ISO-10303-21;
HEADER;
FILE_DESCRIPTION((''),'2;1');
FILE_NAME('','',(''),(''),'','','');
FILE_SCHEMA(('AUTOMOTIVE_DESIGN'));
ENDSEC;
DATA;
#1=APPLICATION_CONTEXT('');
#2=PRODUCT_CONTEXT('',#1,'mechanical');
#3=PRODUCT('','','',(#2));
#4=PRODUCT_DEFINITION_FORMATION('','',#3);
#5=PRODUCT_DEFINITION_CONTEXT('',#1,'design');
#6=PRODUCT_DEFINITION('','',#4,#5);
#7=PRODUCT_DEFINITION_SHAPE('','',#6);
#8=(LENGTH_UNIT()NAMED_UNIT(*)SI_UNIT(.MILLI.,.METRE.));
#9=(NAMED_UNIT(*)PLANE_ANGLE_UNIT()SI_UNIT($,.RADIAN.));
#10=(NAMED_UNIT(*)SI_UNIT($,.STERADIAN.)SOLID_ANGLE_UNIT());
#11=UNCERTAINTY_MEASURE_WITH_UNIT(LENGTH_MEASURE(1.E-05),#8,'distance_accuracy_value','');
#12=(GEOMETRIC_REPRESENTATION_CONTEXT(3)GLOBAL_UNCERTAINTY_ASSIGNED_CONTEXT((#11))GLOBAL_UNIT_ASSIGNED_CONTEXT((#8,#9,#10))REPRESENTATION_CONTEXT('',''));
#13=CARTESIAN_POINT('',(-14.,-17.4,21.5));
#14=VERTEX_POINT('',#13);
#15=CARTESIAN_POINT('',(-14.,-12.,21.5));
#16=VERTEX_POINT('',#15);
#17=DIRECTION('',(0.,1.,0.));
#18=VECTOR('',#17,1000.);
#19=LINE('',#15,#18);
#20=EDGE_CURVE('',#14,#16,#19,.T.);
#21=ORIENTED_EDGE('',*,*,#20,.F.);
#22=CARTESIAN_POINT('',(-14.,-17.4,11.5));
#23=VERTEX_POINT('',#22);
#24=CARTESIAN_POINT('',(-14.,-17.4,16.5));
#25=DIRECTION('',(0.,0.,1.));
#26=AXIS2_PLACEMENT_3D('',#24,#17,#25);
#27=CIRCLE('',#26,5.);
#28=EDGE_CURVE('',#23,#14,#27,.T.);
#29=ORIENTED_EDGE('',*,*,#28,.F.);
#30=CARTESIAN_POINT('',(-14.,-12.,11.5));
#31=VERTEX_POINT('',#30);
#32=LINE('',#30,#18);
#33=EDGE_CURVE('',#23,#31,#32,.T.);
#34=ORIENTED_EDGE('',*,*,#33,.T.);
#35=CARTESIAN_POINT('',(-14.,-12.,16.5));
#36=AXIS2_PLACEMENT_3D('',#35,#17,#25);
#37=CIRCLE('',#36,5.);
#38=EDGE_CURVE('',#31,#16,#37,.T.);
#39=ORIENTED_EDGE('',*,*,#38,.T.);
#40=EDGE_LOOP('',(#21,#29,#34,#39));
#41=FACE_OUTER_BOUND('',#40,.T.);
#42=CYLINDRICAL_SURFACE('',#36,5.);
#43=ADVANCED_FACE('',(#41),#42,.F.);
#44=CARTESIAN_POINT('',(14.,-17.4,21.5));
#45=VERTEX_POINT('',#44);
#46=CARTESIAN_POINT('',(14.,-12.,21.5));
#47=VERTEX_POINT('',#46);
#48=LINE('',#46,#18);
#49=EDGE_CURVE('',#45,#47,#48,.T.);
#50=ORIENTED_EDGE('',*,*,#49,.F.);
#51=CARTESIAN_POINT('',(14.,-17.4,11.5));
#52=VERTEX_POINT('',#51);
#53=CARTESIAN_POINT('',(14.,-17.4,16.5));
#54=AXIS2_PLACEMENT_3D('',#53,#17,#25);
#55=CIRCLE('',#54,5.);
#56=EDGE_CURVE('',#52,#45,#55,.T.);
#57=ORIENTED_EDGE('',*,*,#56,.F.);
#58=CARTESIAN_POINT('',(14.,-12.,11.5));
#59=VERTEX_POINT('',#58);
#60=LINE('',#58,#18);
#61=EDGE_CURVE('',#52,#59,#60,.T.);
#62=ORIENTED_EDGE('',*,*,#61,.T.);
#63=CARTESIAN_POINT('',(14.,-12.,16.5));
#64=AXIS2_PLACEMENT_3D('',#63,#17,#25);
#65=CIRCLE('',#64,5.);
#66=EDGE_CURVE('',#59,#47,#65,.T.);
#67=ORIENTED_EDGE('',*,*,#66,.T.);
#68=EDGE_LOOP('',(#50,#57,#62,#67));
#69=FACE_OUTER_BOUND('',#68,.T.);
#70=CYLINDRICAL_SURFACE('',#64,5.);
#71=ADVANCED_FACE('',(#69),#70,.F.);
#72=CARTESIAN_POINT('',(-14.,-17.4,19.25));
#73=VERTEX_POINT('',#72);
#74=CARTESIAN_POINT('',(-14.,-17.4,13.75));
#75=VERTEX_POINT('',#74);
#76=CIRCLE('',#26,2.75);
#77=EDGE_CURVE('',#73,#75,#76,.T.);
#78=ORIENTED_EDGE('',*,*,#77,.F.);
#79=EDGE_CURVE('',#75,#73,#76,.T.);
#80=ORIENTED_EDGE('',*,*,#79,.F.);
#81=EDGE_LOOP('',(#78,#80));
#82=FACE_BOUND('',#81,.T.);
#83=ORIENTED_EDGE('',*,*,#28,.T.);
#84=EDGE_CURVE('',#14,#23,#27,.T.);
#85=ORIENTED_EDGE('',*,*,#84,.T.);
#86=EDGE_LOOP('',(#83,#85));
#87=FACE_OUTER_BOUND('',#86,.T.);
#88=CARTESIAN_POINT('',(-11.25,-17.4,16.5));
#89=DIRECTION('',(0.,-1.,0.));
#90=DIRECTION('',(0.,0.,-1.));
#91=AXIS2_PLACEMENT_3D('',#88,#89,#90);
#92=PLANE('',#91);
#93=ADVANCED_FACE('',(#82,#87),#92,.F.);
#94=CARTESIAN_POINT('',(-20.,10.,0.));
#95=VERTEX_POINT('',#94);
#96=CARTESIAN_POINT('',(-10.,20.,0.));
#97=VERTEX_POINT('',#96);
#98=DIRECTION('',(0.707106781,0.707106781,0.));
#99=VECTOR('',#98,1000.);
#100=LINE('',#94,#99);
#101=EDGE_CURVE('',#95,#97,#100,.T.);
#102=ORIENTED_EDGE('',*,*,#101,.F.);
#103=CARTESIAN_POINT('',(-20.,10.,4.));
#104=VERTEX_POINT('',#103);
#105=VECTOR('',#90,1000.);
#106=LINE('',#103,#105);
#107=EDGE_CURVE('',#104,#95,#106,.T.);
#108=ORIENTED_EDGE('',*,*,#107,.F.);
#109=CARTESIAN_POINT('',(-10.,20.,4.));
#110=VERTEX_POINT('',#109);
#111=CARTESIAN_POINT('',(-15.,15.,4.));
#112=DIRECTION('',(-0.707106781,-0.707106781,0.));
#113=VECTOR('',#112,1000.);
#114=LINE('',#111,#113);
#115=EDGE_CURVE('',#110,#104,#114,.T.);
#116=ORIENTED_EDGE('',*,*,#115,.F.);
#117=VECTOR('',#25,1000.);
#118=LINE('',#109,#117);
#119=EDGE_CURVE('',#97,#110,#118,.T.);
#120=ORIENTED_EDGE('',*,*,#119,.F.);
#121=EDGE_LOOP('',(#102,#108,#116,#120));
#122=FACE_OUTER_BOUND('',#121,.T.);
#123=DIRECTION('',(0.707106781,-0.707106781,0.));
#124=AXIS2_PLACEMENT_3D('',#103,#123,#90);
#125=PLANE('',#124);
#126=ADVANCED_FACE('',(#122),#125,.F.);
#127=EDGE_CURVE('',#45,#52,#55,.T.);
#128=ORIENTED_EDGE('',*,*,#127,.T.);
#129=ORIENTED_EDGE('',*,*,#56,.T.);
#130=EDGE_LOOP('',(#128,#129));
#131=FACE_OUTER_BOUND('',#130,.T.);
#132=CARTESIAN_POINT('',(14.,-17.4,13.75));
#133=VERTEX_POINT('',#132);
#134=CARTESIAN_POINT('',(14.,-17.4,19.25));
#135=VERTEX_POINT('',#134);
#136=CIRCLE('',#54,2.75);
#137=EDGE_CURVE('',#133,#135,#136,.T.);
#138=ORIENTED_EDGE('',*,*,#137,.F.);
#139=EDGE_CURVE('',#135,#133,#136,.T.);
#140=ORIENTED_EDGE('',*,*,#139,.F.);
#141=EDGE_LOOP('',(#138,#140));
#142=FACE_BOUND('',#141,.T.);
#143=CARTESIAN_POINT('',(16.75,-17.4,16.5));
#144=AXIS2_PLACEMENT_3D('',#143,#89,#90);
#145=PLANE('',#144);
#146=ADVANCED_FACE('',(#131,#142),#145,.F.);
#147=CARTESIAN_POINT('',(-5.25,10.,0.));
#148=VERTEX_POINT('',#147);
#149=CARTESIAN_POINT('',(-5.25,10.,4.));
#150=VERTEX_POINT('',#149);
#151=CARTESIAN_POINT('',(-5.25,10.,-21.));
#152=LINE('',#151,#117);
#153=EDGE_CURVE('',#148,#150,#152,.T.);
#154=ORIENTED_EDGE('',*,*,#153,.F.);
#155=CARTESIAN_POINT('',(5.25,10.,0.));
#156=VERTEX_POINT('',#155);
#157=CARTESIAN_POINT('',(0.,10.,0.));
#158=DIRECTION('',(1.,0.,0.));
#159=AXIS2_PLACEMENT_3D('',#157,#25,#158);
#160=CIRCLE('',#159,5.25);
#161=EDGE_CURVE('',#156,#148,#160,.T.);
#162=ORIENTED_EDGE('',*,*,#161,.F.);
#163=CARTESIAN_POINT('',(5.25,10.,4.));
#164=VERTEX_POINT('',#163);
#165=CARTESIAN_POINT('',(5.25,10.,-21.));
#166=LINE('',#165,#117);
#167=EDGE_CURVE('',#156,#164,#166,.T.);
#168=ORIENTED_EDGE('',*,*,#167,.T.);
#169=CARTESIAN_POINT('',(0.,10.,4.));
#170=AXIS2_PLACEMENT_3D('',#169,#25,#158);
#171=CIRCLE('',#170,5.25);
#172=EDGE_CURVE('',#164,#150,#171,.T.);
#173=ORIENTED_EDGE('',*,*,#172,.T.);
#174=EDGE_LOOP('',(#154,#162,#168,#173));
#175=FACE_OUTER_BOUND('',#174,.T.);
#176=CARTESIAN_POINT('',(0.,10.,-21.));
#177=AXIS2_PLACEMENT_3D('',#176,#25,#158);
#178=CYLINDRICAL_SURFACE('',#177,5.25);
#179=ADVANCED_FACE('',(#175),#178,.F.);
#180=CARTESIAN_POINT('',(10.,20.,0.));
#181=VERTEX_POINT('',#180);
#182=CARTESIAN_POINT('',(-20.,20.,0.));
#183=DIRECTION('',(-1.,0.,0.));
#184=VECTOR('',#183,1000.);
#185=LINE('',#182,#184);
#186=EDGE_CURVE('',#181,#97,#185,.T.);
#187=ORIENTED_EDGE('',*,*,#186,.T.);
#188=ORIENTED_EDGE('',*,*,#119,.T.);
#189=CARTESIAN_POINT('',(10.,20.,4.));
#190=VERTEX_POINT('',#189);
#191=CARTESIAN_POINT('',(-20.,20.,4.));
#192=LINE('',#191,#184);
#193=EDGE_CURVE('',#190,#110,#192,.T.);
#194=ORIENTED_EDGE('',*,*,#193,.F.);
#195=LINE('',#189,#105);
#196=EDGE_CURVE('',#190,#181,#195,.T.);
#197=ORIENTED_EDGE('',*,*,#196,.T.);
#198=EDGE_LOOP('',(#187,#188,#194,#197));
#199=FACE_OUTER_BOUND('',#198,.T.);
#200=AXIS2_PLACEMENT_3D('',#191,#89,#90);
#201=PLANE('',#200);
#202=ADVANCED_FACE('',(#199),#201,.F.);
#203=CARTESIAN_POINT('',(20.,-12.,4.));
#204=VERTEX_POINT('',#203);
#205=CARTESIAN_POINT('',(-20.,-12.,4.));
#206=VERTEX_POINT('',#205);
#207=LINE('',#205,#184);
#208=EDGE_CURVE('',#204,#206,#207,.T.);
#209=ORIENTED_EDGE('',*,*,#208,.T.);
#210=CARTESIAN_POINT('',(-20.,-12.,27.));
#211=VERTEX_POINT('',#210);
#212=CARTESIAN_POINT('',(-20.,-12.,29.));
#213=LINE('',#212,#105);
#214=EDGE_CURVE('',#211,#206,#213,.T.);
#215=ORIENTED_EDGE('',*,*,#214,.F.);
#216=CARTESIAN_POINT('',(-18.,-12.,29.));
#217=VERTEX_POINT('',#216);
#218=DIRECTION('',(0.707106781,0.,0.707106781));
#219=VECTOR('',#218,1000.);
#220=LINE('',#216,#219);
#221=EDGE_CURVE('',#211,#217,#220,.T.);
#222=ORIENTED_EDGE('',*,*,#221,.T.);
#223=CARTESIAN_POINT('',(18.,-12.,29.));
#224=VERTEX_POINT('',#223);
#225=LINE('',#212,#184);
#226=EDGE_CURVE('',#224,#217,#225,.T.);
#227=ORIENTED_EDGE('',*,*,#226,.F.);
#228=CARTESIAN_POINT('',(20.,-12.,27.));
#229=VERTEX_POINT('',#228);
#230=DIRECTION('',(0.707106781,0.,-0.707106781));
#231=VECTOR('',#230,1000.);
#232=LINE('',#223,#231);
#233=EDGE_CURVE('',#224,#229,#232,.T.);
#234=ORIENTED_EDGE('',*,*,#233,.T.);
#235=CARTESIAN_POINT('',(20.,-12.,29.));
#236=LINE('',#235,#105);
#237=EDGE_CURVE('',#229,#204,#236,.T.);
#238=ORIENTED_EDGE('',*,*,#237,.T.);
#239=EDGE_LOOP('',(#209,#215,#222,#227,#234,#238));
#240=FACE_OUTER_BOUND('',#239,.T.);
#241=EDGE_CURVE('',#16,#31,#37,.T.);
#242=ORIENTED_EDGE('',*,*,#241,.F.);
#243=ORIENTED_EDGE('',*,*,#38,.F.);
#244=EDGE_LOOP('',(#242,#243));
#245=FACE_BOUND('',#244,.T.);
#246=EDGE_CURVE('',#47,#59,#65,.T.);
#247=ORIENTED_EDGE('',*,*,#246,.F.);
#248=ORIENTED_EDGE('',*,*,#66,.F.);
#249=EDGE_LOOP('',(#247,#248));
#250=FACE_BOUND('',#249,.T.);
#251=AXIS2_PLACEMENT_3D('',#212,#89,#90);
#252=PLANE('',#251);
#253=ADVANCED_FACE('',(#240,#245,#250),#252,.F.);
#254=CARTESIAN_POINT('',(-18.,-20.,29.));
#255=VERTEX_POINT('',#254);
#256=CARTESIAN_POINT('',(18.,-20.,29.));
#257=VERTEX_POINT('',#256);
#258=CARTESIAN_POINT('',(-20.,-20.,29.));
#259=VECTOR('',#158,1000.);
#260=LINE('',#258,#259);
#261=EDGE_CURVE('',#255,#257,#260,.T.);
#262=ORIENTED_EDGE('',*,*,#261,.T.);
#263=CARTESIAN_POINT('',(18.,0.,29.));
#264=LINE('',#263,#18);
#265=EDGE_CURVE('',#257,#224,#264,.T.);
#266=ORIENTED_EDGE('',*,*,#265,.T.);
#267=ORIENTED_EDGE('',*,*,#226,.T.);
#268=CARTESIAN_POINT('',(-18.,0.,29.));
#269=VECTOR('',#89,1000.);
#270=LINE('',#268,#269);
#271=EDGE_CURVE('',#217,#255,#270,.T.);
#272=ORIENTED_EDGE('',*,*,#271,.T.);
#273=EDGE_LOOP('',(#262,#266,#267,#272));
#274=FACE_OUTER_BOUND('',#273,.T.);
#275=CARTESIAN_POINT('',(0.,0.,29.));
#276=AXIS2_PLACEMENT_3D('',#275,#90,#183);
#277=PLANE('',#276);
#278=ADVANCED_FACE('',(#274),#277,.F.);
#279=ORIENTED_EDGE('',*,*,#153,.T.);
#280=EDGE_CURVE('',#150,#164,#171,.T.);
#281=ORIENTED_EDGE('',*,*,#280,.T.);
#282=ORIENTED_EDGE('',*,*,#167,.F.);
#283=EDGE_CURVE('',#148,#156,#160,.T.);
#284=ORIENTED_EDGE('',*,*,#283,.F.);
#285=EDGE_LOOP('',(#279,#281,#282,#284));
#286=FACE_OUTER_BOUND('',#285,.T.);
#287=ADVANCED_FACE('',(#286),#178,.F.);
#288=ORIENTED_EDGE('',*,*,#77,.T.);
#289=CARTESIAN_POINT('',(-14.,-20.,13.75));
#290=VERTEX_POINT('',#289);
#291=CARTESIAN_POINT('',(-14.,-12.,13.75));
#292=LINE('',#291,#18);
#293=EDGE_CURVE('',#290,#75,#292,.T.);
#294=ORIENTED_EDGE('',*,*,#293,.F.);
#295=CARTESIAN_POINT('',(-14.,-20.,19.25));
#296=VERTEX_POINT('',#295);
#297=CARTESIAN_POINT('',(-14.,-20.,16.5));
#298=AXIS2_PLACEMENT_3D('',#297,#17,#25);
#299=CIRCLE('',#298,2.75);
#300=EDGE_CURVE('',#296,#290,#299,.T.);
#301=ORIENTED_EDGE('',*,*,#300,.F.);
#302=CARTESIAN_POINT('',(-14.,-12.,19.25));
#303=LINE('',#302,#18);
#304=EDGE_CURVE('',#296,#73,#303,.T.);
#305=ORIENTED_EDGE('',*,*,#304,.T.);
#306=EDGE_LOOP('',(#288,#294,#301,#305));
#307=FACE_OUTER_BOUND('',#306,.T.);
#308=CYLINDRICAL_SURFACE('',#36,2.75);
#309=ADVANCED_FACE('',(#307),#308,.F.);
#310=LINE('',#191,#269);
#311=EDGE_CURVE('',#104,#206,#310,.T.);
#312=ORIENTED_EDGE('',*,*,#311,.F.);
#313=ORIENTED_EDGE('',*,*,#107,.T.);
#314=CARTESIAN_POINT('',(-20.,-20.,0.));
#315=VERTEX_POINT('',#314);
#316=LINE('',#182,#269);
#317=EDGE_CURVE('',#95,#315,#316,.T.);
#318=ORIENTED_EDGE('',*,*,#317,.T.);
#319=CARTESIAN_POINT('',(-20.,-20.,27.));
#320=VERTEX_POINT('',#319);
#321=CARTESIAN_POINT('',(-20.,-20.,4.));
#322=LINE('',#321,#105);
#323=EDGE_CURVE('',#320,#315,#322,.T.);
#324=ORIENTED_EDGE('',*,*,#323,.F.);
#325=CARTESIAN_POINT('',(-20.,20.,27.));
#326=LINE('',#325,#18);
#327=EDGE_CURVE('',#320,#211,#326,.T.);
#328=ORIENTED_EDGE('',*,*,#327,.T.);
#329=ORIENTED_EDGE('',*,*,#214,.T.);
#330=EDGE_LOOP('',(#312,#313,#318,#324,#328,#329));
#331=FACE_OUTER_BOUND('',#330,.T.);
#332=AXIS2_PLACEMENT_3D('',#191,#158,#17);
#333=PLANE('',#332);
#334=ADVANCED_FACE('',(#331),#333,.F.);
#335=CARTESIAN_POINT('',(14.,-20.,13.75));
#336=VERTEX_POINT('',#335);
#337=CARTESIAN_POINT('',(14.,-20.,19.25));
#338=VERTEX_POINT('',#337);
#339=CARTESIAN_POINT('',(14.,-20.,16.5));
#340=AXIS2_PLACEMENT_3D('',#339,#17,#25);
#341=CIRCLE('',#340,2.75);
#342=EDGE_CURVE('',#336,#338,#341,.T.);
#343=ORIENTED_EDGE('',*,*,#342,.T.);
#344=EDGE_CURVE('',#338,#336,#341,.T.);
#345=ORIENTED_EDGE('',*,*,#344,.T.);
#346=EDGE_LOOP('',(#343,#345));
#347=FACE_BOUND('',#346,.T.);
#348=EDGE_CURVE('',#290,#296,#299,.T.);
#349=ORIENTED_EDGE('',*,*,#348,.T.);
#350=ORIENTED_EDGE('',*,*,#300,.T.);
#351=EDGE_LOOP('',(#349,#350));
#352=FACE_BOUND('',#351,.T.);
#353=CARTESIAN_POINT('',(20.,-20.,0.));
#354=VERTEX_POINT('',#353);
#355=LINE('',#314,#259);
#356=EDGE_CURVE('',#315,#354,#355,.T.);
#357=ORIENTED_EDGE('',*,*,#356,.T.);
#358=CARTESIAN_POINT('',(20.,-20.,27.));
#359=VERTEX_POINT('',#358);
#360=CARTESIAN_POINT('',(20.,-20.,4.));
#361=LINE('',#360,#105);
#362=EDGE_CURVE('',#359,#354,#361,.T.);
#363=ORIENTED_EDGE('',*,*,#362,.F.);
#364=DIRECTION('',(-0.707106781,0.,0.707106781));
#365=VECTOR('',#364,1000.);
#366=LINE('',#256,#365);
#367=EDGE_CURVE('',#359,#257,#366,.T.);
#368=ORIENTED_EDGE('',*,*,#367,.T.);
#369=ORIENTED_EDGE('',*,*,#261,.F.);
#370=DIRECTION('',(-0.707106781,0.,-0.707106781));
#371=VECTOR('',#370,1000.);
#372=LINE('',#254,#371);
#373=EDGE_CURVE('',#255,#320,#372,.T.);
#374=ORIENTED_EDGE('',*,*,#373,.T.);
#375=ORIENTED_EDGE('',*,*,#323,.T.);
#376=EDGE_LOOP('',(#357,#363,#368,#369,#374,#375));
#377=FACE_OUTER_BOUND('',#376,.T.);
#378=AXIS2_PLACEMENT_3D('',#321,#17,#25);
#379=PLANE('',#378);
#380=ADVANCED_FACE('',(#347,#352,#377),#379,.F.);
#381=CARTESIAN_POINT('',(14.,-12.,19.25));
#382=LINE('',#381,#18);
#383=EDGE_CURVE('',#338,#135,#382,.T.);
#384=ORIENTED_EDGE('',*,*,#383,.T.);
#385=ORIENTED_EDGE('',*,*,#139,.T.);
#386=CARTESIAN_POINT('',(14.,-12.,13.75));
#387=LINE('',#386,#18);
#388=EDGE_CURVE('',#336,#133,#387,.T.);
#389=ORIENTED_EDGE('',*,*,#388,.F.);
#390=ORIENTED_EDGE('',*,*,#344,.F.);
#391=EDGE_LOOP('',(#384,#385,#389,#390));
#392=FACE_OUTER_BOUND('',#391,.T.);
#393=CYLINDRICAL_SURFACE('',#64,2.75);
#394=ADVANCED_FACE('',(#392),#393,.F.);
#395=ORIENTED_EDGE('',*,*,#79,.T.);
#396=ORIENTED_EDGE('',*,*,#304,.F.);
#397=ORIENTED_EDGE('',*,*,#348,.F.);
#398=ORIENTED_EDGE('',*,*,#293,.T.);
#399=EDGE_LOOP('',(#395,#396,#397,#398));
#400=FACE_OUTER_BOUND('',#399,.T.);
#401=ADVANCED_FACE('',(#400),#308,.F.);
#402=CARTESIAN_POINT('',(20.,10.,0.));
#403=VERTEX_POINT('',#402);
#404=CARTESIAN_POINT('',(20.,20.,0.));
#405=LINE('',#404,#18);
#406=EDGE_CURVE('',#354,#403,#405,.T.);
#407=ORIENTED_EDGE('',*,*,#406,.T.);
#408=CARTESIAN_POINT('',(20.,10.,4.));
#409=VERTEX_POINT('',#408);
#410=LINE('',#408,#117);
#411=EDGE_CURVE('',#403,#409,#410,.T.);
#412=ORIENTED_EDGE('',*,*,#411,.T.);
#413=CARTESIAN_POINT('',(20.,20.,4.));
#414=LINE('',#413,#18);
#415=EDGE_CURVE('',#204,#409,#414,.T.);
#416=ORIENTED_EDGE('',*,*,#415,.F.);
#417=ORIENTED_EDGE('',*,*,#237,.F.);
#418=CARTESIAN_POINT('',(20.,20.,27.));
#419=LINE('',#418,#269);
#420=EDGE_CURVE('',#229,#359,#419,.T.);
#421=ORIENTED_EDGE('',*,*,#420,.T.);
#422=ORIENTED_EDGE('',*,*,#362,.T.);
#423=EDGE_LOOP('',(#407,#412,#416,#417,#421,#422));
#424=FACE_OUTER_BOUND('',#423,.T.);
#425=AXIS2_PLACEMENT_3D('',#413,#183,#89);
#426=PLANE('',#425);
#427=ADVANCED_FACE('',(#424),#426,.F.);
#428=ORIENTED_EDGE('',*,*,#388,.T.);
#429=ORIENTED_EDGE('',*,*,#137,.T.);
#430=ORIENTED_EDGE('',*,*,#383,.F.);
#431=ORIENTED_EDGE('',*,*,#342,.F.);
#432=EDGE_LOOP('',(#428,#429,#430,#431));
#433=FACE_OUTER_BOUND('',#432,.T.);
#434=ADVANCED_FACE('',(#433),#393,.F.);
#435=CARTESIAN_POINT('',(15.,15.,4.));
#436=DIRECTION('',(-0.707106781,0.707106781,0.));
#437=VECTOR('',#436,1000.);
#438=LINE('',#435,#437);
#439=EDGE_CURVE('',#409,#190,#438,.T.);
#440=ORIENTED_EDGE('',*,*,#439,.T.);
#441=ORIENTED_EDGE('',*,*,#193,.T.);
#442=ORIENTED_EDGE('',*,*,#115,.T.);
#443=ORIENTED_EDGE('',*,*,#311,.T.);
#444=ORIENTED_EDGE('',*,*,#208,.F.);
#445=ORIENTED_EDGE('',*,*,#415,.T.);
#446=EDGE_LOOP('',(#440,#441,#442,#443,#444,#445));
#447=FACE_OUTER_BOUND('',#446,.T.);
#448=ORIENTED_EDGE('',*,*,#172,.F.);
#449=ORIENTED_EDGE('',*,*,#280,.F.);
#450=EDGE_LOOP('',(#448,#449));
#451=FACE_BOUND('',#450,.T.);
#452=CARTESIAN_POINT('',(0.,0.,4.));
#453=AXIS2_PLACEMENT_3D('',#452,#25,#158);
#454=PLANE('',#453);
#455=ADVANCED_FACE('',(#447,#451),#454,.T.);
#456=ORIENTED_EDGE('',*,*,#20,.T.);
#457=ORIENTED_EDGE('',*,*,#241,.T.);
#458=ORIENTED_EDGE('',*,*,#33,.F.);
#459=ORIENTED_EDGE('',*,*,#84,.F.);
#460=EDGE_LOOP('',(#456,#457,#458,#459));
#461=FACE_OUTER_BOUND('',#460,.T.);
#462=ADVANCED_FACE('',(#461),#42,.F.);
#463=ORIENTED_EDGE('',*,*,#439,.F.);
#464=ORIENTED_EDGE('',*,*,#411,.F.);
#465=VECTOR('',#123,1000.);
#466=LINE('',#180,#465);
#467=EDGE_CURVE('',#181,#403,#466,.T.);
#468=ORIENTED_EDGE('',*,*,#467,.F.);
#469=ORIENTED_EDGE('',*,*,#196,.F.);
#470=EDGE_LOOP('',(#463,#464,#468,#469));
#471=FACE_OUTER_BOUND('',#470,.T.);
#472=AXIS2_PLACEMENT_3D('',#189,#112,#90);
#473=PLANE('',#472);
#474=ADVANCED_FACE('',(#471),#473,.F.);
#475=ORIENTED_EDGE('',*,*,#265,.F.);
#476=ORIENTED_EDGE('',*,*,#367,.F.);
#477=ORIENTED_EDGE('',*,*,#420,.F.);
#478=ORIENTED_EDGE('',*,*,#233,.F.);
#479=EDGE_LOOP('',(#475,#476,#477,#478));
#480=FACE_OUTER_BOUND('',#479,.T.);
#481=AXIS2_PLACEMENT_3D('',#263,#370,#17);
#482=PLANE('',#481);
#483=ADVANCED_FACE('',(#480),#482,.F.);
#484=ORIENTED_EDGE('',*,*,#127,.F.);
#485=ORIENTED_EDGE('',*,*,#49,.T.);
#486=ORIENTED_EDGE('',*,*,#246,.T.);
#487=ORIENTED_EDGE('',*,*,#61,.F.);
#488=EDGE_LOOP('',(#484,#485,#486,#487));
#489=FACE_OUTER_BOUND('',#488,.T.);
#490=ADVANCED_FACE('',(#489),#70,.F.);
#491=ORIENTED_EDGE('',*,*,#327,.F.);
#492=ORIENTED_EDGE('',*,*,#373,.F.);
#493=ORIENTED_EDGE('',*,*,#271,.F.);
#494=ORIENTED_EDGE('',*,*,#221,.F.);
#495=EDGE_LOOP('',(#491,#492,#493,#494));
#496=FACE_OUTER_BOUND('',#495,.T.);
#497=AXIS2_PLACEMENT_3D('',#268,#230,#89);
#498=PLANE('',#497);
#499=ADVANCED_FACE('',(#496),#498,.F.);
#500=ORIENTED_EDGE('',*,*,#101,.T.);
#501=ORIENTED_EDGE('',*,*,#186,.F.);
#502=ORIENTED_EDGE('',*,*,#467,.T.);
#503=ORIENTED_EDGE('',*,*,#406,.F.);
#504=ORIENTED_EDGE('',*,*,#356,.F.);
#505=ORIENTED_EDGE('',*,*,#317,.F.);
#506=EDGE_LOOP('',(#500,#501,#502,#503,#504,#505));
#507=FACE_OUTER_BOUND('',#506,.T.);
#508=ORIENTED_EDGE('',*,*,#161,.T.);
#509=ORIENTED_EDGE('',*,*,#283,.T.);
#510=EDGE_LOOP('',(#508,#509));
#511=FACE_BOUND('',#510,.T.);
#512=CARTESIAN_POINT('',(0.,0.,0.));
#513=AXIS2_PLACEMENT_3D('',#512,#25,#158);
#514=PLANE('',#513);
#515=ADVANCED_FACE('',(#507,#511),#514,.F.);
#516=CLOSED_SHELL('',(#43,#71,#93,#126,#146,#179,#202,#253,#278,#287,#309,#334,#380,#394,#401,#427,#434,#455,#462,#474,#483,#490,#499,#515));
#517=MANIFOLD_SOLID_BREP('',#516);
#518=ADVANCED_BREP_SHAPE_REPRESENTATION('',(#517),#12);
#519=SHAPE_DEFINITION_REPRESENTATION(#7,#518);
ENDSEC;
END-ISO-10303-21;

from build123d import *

# Parameters (mm, degrees)
SKETCH2_W                                           = 40
SKETCH2_H                                           = 40
BOSS_EXTRUDE1_DEPTH                                 = 4
SKETCH3_W                                           = 40
SKETCH3_H                                           = 8
BOSS_EXTRUDE2_DEPTH                                 = 25
SKETCH4_R                                           = 5.25
CUT_EXTRUDE1_DEPTH                                  = 25
CHAMFER1_SIZE                                       = 10
CBORE_FOR_M5_HEX_SOCKET_HEAD_CAP_SCREW1_D           = 5.5
CBORE_FOR_M5_HEX_SOCKET_HEAD_CAP_SCREW1_CBORE_D     = 10
CBORE_FOR_M5_HEX_SOCKET_HEAD_CAP_SCREW1_CBORE_DEPTH = 5.4
CHAMFER2_SIZE                                       = 2


with BuildPart() as part:
    # Sketch2 → Boss-Extrude1 (new body)
    with BuildSketch(Plane.XY):
        Rectangle(SKETCH2_W, SKETCH2_H)
    extrude(amount=BOSS_EXTRUDE1_DEPTH)

    # Sketch3 → Boss-Extrude2 (add)
    with BuildSketch(Plane.XY.offset(4)):
        with Locations((0, -16)):
            Rectangle(SKETCH3_W, SKETCH3_H)
    extrude(amount=BOSS_EXTRUDE2_DEPTH)

    # Sketch4 → Cut-Extrude1 (cut)
    with BuildSketch(Plane.XY.offset(4)):
        with Locations((0, 10)):
            Circle(SKETCH4_R)
    extrude(amount=-CUT_EXTRUDE1_DEPTH, mode=Mode.SUBTRACT)

    # Chamfer1
    chamfer1_edges = [part.edges().sort_by_distance(p)[0] for p in [
        (20, 20, 2),
        (-20, 20, 2),
    ]]
    chamfer(chamfer1_edges, length=CHAMFER1_SIZE)

    # CBORE for M5 Hex Socket Head Cap Screw1 (through all)
    with Locations(Plane(origin=(0, -12, 0), x_dir=(1, 0, 0), z_dir=(0, 1, 0))):
        with Locations((-14, -16.5), (14, -16.5)):
            CounterBoreHole(CBORE_FOR_M5_HEX_SOCKET_HEAD_CAP_SCREW1_D / 2, CBORE_FOR_M5_HEX_SOCKET_HEAD_CAP_SCREW1_CBORE_D / 2, CBORE_FOR_M5_HEX_SOCKET_HEAD_CAP_SCREW1_CBORE_DEPTH)

    # Chamfer2
    chamfer2_edges = [part.edges().sort_by_distance(p)[0] for p in [
        (20, -16, 29),
        (-20, -16, 29),
    ]]
    chamfer(chamfer2_edges, length=CHAMFER2_SIZE)


solid = part.part
